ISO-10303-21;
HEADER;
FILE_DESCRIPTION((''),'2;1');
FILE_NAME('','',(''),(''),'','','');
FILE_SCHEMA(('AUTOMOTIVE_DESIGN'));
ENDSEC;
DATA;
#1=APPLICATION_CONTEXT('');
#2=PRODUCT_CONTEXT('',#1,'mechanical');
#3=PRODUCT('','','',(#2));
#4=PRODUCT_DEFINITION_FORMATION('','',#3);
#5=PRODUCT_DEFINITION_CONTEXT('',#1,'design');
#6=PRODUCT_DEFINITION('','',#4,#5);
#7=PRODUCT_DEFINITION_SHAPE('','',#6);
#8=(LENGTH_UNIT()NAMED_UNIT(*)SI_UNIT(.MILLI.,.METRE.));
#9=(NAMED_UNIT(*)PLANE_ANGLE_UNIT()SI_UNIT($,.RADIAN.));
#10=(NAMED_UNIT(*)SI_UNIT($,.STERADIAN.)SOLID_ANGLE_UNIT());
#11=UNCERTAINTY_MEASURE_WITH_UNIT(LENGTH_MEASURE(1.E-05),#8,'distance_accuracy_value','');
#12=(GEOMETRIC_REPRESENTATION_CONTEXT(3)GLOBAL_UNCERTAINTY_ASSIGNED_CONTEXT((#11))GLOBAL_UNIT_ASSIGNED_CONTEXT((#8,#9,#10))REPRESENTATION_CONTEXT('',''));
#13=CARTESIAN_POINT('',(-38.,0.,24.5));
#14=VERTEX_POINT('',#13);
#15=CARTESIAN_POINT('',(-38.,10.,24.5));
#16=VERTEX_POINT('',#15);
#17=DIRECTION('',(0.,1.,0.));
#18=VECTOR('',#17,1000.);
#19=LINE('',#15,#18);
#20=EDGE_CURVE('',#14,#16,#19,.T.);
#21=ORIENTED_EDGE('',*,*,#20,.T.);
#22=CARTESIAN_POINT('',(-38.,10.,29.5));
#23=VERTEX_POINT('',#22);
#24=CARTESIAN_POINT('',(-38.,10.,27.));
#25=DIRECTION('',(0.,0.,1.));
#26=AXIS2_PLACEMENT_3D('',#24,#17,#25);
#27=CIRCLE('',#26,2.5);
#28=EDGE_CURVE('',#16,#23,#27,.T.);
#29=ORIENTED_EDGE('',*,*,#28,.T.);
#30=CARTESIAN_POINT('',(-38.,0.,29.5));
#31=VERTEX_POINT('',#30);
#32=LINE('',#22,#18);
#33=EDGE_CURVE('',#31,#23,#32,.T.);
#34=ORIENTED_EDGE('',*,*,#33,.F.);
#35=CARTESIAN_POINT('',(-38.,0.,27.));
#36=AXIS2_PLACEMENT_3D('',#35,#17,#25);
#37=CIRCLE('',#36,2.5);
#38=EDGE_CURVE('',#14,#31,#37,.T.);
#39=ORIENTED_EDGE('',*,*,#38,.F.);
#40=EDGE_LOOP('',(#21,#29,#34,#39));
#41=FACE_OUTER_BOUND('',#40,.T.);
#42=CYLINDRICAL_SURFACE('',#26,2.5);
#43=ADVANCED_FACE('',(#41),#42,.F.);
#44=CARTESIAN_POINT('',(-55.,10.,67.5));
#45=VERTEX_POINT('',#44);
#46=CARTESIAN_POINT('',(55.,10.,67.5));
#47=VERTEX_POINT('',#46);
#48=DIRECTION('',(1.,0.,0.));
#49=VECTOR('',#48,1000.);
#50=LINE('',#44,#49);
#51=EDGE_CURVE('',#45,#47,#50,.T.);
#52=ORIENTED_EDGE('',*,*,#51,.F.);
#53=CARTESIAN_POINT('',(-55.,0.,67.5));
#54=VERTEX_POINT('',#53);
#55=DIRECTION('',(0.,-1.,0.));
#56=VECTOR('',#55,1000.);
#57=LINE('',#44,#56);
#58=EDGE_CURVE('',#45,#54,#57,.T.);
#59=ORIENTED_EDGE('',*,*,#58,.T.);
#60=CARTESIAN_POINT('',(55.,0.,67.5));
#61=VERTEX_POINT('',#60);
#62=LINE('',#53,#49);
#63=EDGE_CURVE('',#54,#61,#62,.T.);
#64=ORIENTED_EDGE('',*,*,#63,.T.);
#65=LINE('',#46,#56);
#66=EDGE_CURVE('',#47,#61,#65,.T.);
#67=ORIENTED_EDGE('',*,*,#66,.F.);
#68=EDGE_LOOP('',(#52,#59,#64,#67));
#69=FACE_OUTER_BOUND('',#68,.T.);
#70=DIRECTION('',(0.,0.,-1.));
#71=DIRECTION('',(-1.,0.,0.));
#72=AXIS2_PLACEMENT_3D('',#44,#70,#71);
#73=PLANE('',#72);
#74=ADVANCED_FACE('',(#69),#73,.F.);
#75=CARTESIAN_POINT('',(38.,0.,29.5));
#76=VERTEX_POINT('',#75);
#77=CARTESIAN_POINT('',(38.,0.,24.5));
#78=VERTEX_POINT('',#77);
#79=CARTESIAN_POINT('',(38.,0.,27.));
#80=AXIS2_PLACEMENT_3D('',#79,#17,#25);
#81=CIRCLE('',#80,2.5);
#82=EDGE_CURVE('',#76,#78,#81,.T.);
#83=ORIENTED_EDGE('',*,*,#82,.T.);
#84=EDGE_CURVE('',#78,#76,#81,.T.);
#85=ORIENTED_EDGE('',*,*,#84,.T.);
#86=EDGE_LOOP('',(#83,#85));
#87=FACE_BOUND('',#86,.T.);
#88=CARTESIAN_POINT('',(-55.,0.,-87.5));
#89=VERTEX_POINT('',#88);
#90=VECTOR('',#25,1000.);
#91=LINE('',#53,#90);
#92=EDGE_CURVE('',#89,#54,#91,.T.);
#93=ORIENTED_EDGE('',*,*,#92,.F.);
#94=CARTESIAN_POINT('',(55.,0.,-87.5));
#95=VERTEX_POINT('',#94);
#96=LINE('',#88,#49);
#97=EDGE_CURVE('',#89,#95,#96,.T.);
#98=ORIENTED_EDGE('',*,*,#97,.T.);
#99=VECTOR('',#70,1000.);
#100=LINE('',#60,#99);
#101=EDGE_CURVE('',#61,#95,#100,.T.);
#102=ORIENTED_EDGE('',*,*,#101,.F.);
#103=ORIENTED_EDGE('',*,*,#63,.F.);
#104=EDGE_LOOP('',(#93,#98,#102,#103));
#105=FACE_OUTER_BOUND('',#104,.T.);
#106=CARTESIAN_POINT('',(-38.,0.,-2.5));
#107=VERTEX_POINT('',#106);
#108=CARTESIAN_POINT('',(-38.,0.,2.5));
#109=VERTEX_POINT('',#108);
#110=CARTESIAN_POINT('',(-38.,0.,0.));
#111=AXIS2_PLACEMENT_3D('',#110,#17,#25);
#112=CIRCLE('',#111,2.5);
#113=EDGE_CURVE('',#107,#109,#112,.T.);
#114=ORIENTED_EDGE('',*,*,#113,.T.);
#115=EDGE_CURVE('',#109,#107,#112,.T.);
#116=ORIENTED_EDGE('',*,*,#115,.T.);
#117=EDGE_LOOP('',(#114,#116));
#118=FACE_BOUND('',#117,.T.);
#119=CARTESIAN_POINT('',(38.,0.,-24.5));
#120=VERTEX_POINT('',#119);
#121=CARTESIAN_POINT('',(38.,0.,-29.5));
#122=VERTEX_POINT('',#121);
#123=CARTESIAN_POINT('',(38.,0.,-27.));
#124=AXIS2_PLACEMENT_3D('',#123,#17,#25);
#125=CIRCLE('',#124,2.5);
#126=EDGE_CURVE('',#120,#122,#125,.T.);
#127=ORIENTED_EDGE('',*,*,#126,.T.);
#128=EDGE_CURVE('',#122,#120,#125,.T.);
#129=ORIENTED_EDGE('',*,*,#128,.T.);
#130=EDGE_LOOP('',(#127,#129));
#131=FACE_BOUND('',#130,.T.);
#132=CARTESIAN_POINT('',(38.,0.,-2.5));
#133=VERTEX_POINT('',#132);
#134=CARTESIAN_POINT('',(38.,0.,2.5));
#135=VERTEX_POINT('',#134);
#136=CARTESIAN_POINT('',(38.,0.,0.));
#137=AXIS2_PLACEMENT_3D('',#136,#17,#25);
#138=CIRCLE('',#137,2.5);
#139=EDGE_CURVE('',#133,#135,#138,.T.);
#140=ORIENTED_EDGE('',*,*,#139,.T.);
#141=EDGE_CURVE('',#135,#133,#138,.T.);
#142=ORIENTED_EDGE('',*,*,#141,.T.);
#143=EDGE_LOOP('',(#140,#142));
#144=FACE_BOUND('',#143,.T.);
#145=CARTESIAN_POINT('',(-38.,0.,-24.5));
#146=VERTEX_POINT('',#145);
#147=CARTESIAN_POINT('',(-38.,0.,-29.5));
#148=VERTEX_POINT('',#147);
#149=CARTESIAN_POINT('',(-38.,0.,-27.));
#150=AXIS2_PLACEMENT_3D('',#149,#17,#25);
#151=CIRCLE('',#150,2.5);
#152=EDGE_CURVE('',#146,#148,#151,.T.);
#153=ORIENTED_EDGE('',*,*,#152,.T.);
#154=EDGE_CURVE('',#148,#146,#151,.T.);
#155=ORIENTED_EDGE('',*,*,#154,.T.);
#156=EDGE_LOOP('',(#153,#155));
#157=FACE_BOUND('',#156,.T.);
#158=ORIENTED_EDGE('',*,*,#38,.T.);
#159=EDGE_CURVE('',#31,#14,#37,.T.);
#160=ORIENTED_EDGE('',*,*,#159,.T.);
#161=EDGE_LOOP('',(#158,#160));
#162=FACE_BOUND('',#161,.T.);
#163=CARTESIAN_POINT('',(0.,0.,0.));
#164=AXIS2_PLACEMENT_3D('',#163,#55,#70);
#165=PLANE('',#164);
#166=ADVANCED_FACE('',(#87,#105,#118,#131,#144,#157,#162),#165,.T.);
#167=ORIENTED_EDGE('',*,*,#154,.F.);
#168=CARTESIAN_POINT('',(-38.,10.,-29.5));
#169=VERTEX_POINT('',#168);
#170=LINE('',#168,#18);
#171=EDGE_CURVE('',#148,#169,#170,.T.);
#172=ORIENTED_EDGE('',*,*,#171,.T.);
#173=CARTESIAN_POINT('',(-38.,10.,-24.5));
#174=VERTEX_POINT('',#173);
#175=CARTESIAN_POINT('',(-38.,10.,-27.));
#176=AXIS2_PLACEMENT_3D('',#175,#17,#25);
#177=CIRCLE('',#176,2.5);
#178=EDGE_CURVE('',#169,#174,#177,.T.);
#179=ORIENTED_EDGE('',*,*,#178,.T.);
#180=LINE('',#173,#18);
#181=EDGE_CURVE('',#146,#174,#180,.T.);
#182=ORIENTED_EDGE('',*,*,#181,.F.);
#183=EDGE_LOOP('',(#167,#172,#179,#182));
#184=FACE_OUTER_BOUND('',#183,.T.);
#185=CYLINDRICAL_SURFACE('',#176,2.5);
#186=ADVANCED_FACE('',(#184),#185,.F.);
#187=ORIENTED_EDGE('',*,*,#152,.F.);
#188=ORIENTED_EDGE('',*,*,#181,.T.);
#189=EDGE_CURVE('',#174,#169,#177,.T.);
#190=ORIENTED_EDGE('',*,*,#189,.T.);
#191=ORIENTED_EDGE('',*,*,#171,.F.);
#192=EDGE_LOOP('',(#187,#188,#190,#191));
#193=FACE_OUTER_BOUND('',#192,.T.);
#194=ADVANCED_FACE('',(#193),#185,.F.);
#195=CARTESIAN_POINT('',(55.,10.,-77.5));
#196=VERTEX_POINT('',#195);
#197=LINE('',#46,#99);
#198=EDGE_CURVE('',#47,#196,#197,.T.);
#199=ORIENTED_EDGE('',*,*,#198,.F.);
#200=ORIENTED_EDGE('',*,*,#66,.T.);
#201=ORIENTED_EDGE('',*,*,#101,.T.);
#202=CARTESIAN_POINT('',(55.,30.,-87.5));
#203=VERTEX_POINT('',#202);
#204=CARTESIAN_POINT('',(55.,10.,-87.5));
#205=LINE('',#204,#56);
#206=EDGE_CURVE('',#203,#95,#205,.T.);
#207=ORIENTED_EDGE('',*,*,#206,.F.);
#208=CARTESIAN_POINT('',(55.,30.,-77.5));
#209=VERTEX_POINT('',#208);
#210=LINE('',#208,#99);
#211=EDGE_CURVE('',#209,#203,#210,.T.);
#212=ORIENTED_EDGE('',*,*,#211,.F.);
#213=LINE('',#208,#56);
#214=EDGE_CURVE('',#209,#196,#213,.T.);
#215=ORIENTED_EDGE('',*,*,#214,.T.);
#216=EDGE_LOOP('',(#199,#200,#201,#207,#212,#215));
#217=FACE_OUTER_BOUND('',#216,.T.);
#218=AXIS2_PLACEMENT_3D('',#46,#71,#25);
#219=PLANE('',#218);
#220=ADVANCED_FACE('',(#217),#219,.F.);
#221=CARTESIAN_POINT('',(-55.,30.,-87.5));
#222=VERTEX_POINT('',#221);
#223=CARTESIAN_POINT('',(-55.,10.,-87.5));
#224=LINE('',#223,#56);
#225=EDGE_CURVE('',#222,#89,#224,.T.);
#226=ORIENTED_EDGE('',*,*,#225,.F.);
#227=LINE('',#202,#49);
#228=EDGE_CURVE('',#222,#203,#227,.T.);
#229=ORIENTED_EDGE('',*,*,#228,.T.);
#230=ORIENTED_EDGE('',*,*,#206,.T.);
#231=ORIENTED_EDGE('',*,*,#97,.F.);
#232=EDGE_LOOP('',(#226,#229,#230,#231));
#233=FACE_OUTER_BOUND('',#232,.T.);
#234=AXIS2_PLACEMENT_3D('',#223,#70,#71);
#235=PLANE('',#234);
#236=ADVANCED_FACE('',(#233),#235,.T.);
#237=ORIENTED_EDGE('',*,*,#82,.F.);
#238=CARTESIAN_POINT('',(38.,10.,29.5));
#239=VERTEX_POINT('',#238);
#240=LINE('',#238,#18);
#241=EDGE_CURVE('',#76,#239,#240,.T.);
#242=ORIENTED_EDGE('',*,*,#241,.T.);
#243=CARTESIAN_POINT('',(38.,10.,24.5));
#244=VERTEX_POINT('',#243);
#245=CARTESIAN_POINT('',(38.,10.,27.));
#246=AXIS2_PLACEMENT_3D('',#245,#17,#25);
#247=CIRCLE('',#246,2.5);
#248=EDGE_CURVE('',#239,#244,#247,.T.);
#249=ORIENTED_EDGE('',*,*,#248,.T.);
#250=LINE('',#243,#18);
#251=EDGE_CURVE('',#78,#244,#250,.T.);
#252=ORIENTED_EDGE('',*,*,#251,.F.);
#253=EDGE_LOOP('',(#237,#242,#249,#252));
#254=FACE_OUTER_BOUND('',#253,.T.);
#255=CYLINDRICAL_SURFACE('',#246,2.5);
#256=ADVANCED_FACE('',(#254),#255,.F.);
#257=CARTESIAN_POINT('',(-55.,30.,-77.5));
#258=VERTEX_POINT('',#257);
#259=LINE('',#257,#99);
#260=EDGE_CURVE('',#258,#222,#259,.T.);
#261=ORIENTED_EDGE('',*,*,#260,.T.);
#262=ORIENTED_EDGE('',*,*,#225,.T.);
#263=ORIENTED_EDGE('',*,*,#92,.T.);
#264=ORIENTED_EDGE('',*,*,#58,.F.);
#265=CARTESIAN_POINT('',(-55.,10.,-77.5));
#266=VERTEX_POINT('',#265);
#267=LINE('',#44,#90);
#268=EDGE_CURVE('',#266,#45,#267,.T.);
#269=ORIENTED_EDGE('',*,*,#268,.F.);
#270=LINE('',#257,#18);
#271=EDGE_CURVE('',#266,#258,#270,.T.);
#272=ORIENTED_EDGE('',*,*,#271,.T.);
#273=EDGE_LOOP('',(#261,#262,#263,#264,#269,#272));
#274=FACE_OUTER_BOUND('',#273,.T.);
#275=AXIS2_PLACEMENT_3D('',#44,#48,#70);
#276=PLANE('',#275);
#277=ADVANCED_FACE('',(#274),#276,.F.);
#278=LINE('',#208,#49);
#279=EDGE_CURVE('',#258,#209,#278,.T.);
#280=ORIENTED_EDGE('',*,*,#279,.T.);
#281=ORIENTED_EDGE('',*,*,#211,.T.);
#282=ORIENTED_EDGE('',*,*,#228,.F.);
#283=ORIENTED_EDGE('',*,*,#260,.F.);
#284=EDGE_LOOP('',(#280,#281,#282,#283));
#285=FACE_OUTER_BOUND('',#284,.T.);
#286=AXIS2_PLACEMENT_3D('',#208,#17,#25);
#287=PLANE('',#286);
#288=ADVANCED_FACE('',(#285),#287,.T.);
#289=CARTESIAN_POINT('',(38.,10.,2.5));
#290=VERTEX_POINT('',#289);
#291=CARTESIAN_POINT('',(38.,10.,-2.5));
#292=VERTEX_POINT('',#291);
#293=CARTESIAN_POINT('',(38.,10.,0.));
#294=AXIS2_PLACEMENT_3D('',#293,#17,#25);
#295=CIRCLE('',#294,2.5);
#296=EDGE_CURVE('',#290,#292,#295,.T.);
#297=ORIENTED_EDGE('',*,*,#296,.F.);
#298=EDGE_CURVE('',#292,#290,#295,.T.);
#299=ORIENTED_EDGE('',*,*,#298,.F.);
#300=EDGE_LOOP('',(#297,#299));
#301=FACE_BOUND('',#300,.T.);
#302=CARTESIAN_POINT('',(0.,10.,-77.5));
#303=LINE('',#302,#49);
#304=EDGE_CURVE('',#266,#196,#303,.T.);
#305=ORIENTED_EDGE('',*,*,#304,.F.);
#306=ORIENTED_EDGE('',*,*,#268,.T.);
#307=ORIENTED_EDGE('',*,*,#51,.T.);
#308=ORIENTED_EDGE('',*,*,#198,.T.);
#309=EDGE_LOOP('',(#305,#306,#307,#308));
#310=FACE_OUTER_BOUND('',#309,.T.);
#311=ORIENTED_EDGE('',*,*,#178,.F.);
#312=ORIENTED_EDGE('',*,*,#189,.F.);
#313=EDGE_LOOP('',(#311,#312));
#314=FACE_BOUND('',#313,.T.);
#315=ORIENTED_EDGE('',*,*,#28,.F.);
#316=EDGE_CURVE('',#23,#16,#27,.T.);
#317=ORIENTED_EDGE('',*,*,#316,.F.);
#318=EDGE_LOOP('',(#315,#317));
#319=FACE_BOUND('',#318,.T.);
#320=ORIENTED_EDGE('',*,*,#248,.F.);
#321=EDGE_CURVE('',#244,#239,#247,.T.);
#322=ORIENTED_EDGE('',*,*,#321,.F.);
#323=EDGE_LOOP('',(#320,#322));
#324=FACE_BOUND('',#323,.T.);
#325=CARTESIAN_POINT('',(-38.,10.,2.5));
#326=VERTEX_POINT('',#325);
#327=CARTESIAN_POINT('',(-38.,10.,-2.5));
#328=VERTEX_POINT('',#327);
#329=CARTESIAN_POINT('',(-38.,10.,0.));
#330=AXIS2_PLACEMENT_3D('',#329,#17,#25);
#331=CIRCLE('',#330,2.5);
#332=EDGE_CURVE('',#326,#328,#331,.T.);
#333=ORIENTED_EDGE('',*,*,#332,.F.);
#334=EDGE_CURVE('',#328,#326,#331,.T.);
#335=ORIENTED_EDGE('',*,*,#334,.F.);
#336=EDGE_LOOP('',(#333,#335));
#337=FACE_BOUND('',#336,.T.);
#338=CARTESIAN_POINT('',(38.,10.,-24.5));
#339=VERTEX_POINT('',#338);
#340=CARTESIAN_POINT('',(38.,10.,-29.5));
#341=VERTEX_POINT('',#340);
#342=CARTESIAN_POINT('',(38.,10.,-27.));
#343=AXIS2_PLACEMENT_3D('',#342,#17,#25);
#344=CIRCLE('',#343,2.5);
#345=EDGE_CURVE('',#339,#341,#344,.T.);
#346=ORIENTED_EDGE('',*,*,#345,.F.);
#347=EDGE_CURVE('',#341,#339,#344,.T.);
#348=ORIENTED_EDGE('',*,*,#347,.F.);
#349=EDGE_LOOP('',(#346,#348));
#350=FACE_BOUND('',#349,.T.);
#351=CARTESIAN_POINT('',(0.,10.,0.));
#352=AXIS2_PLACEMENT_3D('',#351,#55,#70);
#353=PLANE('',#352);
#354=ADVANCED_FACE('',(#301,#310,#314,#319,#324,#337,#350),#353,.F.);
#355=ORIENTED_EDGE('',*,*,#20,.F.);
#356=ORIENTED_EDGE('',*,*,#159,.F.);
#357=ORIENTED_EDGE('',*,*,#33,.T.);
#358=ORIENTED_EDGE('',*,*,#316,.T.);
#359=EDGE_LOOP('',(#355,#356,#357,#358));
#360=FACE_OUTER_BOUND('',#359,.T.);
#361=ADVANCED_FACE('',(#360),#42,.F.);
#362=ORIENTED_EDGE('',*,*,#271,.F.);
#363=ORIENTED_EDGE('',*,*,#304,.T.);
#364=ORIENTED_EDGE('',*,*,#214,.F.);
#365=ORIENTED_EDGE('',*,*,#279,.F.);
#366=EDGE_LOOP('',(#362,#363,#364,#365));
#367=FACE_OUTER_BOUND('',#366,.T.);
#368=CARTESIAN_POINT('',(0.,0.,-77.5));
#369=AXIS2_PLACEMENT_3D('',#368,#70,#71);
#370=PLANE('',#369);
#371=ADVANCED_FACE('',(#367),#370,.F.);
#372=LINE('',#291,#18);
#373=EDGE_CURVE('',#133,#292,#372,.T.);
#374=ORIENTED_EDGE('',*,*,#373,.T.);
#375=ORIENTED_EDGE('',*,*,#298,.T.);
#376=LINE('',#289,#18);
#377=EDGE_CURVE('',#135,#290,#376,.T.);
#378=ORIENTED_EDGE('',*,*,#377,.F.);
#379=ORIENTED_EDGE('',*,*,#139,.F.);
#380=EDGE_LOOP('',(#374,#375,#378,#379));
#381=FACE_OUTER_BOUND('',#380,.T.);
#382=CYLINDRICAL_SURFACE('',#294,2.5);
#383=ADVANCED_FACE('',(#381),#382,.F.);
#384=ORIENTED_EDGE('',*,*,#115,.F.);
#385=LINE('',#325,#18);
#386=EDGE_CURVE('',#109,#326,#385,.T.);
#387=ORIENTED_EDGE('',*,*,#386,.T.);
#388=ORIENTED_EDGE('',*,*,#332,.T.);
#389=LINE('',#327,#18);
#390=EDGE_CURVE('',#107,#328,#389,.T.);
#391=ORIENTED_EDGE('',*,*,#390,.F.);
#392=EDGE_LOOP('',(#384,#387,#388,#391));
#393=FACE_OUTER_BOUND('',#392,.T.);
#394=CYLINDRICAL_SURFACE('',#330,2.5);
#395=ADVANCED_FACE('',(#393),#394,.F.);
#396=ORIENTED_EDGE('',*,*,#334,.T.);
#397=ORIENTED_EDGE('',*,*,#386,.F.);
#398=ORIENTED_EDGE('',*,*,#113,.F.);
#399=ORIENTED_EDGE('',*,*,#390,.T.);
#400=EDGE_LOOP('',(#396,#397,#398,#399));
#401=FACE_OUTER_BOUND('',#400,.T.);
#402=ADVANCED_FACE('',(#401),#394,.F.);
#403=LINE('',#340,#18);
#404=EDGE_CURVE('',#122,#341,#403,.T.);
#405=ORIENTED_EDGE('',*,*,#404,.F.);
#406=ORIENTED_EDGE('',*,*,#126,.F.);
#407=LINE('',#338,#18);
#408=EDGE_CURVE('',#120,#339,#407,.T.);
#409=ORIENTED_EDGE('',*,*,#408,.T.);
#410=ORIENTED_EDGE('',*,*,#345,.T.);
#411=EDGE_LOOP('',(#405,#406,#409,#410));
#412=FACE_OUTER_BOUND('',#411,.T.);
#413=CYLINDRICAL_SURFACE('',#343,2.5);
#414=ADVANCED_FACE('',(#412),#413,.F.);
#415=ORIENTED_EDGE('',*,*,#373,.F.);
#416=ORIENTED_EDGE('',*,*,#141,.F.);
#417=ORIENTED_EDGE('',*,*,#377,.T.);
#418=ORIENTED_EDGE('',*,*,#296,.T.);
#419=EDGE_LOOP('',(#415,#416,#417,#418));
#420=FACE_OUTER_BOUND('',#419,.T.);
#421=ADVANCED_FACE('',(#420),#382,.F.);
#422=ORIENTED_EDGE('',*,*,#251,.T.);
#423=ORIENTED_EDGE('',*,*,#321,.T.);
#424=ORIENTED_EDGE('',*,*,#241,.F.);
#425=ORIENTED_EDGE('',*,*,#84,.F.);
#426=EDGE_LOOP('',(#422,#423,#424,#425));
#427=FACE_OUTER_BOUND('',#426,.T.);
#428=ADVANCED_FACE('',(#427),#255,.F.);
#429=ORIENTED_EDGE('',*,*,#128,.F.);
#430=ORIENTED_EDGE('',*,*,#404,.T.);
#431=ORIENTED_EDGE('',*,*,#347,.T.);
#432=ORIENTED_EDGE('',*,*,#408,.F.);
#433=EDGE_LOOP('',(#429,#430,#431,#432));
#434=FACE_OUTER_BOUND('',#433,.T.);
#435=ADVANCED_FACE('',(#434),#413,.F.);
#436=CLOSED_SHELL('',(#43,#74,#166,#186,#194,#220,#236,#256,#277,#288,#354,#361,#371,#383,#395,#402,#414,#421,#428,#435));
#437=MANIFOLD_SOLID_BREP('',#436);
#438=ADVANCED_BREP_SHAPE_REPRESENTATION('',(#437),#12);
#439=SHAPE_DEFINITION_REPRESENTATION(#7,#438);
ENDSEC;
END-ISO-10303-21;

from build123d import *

# Parameters (mm, degrees)
SKETCH_2_W         = 110
SKETCH_2_H         = 135
EXTRUDE_1_DEPTH    = 10
HOLE_WIZARD_M6_1_D = 5
SKETCH_11_W        = 110
SKETCH_11_H        = 20
EXTRUDE_6_DEPTH    = 10
SKETCH_15_W        = 110
SKETCH_15_H        = 30
EXTRUDE_7_DEPTH    = 10


with BuildPart() as part:
    # 草图2 → 凸台-拉伸1 (new body)
    with BuildSketch(Plane(origin=(0, 0, 0), x_dir=(1, 0, 0), z_dir=(0, 1, 0))):
        Rectangle(SKETCH_2_W, SKETCH_2_H)
    extrude(amount=EXTRUDE_1_DEPTH)

    # M6 螺纹孔1 (through all)
    with Locations(Plane(origin=(0, 10, 0), x_dir=(1, 0, 0), z_dir=(0, 1, 0))):
        with Locations((-38, 27), (-38, 0), (38, 0), (-38, -27), (38, -27), (38, 27)):
            Hole(HOLE_WIZARD_M6_1_D / 2)

    # 草图11 → 凸台-拉伸6 (add)
    with BuildSketch(Plane.XZ):
        with Locations((0, -77.5)):
            Rectangle(SKETCH_11_W, SKETCH_11_H)
    extrude(amount=-EXTRUDE_6_DEPTH)

    # 草图15 → 凸台-拉伸7 (add)
    with BuildSketch(Plane(origin=(0, 0, -87.5), x_dir=(-1, 0, 0), z_dir=(0, 0, -1))):
        with Locations((0, 15)):
            Rectangle(SKETCH_15_W, SKETCH_15_H)
    extrude(amount=-EXTRUDE_7_DEPTH)


solid = part.part
